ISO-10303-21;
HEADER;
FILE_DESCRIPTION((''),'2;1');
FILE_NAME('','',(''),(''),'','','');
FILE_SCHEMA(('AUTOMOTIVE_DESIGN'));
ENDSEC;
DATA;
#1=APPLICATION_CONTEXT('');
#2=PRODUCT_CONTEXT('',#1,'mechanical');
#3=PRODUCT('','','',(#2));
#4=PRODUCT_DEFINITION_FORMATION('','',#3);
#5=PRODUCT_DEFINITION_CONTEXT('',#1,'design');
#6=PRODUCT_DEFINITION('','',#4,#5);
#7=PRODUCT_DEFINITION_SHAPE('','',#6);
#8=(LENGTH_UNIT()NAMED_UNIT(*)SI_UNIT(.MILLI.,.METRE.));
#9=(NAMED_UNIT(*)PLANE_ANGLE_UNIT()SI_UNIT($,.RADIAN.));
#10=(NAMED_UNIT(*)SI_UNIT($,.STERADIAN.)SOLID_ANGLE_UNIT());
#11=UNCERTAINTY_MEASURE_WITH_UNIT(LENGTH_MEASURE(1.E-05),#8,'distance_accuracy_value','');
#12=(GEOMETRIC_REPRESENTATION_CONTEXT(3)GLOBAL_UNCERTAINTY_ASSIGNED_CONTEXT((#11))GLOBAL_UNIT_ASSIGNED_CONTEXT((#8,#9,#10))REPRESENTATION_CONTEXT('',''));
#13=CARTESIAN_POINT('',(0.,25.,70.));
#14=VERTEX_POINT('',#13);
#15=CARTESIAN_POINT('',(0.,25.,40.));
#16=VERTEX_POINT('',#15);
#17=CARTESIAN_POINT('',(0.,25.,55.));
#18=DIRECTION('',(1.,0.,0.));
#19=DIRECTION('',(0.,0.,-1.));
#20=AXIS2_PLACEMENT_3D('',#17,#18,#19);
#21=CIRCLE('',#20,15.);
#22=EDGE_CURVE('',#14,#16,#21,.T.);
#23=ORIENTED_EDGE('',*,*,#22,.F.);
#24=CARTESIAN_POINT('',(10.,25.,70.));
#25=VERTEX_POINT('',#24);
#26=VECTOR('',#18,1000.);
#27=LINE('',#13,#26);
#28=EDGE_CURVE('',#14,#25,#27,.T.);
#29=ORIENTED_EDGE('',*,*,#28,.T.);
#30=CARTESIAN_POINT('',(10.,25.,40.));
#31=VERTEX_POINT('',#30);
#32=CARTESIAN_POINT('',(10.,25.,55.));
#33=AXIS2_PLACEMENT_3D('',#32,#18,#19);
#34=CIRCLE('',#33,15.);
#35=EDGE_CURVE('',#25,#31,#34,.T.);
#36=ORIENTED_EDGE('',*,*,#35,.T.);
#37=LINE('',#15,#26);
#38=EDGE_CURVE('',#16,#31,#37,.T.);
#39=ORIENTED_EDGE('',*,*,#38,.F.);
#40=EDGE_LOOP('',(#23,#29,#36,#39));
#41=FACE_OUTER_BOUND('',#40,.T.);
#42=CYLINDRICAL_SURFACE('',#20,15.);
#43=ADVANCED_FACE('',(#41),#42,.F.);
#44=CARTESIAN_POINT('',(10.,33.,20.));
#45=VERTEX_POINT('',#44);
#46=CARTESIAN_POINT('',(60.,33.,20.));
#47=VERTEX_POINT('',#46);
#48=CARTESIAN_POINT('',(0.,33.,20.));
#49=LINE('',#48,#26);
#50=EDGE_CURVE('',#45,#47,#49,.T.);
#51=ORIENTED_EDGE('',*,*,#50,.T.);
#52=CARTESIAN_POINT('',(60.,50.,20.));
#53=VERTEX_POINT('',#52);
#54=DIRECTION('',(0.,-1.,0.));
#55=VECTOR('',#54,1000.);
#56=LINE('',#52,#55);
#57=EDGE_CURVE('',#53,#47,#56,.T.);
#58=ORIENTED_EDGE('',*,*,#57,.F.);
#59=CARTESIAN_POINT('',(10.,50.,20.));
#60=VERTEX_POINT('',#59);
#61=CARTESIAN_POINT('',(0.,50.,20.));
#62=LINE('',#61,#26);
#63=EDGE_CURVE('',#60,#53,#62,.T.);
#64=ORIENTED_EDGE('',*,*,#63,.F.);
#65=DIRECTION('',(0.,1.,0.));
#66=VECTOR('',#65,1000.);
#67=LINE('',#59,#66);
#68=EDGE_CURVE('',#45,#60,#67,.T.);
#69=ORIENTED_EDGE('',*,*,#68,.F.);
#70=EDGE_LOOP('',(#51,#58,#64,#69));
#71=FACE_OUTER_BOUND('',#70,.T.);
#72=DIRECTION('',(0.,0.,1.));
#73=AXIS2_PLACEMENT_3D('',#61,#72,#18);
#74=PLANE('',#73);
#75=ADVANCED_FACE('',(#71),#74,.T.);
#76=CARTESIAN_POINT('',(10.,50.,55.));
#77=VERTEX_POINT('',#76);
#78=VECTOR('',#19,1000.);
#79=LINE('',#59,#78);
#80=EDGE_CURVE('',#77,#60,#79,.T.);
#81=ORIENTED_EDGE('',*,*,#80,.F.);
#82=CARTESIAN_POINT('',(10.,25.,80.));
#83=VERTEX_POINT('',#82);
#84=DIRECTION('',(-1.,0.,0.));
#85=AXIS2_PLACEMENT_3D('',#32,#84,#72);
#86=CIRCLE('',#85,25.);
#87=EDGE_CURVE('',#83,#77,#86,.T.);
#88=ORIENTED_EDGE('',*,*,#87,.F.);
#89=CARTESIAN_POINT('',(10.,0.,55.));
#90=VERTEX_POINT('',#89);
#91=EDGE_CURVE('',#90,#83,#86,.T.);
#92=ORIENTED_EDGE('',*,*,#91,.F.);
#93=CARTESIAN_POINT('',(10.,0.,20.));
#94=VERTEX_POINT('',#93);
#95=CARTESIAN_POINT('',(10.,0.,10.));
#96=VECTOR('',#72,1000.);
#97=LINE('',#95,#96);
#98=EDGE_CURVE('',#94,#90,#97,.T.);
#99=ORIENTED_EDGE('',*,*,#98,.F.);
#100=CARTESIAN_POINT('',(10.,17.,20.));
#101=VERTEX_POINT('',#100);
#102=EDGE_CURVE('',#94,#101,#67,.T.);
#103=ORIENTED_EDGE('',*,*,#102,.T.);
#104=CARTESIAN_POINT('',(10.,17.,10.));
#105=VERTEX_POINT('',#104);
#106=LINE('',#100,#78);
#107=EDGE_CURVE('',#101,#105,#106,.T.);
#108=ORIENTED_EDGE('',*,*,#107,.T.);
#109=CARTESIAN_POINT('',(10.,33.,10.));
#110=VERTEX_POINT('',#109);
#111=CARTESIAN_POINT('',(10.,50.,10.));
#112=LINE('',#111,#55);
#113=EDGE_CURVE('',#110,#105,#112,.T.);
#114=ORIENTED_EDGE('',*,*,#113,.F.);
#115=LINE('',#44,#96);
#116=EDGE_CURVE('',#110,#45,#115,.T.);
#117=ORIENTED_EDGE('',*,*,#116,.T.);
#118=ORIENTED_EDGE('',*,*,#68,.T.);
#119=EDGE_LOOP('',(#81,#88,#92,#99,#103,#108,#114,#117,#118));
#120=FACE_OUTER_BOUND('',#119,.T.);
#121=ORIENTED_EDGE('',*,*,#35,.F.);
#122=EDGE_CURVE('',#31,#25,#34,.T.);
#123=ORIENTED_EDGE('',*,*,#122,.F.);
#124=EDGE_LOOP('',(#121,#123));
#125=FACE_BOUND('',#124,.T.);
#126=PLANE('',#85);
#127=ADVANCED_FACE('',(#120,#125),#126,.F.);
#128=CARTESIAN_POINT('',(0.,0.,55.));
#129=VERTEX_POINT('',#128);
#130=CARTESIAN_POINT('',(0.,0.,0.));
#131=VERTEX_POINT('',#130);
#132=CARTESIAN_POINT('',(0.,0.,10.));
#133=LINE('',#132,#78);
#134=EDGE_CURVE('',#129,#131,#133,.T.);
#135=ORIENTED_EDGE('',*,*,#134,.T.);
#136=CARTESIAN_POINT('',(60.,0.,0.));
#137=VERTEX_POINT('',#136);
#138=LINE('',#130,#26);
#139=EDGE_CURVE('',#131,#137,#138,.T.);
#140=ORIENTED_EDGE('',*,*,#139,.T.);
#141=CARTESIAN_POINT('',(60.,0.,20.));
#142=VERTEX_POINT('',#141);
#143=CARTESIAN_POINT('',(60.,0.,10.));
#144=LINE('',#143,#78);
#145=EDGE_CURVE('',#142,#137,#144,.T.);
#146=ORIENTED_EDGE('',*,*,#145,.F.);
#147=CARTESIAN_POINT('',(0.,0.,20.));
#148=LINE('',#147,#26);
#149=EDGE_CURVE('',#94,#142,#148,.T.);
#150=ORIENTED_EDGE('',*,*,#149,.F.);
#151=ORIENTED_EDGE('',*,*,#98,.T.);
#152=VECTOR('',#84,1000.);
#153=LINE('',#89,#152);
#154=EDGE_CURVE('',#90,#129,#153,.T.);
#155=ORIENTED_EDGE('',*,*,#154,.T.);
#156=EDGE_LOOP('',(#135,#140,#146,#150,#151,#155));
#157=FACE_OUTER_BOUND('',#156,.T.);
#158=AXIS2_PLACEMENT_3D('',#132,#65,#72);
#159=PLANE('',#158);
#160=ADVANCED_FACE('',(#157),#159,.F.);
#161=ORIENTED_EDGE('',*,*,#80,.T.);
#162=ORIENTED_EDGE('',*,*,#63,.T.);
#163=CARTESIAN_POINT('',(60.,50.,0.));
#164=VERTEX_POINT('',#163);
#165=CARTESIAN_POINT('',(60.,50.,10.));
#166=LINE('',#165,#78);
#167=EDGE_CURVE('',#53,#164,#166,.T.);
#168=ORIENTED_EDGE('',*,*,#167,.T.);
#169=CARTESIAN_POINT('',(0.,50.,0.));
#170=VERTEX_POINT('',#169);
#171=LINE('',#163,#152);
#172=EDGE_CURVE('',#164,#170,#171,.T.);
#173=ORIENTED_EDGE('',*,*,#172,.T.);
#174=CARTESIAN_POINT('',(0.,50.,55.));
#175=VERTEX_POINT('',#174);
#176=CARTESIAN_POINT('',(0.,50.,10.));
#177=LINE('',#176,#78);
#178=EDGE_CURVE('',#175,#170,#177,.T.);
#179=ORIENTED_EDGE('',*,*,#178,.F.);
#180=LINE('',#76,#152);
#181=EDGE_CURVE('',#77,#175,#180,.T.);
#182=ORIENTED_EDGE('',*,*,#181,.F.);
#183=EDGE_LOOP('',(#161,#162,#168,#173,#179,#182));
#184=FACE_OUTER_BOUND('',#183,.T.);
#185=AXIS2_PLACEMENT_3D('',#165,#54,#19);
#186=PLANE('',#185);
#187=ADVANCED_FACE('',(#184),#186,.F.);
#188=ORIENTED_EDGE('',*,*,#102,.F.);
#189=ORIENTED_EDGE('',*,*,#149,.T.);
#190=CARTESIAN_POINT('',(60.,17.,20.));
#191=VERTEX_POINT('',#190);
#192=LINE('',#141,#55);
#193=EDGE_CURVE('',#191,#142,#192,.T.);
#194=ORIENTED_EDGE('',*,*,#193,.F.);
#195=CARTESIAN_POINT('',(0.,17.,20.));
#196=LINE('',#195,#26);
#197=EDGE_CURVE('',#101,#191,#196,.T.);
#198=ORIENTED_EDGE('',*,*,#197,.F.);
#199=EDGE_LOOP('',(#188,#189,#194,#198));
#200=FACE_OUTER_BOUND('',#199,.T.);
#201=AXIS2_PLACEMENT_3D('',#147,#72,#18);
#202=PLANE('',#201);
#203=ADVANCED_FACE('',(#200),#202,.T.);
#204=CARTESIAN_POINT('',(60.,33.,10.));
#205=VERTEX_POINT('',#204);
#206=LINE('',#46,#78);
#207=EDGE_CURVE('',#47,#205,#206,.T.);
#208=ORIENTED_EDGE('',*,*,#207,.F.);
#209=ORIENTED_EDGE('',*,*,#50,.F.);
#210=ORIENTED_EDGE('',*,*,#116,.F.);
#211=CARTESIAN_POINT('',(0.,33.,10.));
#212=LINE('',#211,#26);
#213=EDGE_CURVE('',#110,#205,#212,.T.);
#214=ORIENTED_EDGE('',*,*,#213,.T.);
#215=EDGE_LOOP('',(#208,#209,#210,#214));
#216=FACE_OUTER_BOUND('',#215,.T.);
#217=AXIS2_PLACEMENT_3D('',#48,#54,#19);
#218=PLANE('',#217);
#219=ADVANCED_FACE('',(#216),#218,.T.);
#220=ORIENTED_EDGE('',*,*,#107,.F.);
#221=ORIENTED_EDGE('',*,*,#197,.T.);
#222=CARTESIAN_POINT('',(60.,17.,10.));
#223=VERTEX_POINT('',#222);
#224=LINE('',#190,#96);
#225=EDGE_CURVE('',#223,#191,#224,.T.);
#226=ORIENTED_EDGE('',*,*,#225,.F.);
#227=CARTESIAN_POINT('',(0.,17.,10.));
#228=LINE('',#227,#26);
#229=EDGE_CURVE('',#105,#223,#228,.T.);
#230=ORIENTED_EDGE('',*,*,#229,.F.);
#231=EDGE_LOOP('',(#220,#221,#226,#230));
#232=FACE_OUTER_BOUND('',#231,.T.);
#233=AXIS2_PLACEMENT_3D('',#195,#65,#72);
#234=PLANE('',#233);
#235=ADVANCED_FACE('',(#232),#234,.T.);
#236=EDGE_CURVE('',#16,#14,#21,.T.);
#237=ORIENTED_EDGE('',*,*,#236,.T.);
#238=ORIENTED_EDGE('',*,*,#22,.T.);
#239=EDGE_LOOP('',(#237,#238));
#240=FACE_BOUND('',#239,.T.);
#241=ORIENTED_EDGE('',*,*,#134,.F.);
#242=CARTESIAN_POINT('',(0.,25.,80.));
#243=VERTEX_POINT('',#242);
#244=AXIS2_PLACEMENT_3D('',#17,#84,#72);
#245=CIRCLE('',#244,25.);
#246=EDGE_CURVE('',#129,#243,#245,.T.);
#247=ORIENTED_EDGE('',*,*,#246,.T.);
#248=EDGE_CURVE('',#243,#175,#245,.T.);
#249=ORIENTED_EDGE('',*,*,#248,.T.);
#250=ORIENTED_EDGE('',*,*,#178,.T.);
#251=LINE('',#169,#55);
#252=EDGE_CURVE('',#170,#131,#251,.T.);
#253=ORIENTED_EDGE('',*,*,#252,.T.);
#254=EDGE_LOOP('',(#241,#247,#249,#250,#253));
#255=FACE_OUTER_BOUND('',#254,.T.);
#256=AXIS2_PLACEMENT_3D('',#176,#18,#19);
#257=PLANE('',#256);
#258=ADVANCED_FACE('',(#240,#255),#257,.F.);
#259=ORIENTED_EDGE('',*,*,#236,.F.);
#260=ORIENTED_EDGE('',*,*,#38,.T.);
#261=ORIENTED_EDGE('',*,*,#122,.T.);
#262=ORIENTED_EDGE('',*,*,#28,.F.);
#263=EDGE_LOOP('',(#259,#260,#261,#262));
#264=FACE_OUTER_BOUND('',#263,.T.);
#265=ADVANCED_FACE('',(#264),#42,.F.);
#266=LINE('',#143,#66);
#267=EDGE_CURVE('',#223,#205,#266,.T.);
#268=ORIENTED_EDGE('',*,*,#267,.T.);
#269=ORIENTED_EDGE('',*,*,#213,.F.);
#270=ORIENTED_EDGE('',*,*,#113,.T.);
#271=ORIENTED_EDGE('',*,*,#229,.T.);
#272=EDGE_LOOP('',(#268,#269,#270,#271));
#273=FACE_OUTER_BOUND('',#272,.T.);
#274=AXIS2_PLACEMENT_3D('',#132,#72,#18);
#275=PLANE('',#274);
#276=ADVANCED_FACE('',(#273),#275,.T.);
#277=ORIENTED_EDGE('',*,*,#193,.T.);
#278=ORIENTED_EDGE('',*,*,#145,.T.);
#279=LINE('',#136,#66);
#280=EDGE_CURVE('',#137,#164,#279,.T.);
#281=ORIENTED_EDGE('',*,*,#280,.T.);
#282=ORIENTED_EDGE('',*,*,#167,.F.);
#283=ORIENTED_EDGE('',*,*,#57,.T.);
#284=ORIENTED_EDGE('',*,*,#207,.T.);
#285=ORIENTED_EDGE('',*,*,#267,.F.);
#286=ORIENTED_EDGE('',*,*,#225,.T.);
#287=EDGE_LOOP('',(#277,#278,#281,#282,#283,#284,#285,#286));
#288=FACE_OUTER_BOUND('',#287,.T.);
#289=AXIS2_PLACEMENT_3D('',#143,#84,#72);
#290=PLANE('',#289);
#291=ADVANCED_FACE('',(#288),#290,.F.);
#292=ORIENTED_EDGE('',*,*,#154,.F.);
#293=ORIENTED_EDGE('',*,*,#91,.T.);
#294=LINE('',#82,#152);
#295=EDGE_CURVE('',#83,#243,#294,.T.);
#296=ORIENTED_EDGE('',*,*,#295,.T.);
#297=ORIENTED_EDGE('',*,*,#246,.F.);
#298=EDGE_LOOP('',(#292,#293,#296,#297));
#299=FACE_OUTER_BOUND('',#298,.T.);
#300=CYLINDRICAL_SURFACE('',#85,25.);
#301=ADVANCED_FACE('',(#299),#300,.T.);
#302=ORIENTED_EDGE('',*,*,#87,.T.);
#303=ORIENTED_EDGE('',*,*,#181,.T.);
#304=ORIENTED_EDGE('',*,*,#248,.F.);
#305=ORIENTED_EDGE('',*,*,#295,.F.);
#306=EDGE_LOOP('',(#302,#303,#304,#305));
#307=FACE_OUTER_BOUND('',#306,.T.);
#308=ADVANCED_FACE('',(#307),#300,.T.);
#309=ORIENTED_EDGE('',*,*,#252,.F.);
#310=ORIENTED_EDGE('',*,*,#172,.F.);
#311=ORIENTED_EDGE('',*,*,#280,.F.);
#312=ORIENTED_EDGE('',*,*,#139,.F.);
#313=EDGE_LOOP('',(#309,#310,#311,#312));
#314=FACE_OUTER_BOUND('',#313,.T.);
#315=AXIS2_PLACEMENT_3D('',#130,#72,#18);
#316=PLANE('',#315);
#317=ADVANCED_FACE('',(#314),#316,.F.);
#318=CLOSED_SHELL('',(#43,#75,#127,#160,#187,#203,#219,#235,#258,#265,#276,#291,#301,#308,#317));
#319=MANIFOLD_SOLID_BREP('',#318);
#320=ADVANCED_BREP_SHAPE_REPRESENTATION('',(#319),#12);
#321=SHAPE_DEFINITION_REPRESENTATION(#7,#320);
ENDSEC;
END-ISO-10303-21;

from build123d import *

# Parameters (mm, degrees)
BASE_PLATE_SKETCH_W    = 60
BASE_PLATE_SKETCH_H    = 50
BASE_PLATE_DEPTH       = 10
UPRIGHT_BLOCK_SKETCH_W = 10
UPRIGHT_BLOCK_SKETCH_H = 17
UPRIGHT_BLOCK_DEPTH    = 60
BLOCK_SLOT_SKETCH_W    = 10
BLOCK_SLOT_SKETCH_H    = 50
BLOCK_SLOT_DEPTH       = 10
ROUNDED_LUG_DEPTH      = 10
LUG_HOLE_SKETCH_R      = 15
LUG_HOLE_DEPTH         = 10


with BuildPart() as part:
    # Base Plate Sketch → Base Plate (new body)
    with BuildSketch(Plane.XY):
        with Locations((30, 25)):
            Rectangle(BASE_PLATE_SKETCH_W, BASE_PLATE_SKETCH_H)
    extrude(amount=BASE_PLATE_DEPTH)

    # Upright Block Sketch → Upright Block (add)
    with BuildSketch(Plane(origin=(60, 0, 0), x_dir=(0, 0, -1), z_dir=(1, 0, 0))):
        with Locations((-15, 41.5)):
            Rectangle(UPRIGHT_BLOCK_SKETCH_W, UPRIGHT_BLOCK_SKETCH_H)
        with Locations((-15, 8.5)):
            Rectangle(UPRIGHT_BLOCK_SKETCH_W, UPRIGHT_BLOCK_SKETCH_H)
    extrude(amount=-UPRIGHT_BLOCK_DEPTH)

    # Block Slot Sketch → Block Slot (cut)
    with BuildSketch(Plane.XY.offset(20)):
        with Locations((5, 25)):
            Rectangle(BLOCK_SLOT_SKETCH_W, BLOCK_SLOT_SKETCH_H)
    extrude(amount=-BLOCK_SLOT_DEPTH, mode=Mode.SUBTRACT)

    # Rounded Lug Sketch → Rounded Lug (add)
    with BuildSketch(Plane.ZY):
        with BuildLine():
            Line((20, 50), (10, 50))
            Line((10, 50), (10, 0))
            Line((10, 0), (20, 0))
            Line((20, 0), (55, 0))
            ThreePointArc((55, 0), (80, 25), (55, 50))
            Line((55, 50), (20, 50))
        make_face()
    extrude(amount=-ROUNDED_LUG_DEPTH)

    # Lug Hole Sketch → Lug Hole (cut)
    with BuildSketch(Plane(origin=(10, 0, 0), x_dir=(0, 0, -1), z_dir=(1, 0, 0))):
        with Locations((-55, 25)):
            Circle(LUG_HOLE_SKETCH_R)
    extrude(amount=-LUG_HOLE_DEPTH, mode=Mode.SUBTRACT)


solid = part.part
